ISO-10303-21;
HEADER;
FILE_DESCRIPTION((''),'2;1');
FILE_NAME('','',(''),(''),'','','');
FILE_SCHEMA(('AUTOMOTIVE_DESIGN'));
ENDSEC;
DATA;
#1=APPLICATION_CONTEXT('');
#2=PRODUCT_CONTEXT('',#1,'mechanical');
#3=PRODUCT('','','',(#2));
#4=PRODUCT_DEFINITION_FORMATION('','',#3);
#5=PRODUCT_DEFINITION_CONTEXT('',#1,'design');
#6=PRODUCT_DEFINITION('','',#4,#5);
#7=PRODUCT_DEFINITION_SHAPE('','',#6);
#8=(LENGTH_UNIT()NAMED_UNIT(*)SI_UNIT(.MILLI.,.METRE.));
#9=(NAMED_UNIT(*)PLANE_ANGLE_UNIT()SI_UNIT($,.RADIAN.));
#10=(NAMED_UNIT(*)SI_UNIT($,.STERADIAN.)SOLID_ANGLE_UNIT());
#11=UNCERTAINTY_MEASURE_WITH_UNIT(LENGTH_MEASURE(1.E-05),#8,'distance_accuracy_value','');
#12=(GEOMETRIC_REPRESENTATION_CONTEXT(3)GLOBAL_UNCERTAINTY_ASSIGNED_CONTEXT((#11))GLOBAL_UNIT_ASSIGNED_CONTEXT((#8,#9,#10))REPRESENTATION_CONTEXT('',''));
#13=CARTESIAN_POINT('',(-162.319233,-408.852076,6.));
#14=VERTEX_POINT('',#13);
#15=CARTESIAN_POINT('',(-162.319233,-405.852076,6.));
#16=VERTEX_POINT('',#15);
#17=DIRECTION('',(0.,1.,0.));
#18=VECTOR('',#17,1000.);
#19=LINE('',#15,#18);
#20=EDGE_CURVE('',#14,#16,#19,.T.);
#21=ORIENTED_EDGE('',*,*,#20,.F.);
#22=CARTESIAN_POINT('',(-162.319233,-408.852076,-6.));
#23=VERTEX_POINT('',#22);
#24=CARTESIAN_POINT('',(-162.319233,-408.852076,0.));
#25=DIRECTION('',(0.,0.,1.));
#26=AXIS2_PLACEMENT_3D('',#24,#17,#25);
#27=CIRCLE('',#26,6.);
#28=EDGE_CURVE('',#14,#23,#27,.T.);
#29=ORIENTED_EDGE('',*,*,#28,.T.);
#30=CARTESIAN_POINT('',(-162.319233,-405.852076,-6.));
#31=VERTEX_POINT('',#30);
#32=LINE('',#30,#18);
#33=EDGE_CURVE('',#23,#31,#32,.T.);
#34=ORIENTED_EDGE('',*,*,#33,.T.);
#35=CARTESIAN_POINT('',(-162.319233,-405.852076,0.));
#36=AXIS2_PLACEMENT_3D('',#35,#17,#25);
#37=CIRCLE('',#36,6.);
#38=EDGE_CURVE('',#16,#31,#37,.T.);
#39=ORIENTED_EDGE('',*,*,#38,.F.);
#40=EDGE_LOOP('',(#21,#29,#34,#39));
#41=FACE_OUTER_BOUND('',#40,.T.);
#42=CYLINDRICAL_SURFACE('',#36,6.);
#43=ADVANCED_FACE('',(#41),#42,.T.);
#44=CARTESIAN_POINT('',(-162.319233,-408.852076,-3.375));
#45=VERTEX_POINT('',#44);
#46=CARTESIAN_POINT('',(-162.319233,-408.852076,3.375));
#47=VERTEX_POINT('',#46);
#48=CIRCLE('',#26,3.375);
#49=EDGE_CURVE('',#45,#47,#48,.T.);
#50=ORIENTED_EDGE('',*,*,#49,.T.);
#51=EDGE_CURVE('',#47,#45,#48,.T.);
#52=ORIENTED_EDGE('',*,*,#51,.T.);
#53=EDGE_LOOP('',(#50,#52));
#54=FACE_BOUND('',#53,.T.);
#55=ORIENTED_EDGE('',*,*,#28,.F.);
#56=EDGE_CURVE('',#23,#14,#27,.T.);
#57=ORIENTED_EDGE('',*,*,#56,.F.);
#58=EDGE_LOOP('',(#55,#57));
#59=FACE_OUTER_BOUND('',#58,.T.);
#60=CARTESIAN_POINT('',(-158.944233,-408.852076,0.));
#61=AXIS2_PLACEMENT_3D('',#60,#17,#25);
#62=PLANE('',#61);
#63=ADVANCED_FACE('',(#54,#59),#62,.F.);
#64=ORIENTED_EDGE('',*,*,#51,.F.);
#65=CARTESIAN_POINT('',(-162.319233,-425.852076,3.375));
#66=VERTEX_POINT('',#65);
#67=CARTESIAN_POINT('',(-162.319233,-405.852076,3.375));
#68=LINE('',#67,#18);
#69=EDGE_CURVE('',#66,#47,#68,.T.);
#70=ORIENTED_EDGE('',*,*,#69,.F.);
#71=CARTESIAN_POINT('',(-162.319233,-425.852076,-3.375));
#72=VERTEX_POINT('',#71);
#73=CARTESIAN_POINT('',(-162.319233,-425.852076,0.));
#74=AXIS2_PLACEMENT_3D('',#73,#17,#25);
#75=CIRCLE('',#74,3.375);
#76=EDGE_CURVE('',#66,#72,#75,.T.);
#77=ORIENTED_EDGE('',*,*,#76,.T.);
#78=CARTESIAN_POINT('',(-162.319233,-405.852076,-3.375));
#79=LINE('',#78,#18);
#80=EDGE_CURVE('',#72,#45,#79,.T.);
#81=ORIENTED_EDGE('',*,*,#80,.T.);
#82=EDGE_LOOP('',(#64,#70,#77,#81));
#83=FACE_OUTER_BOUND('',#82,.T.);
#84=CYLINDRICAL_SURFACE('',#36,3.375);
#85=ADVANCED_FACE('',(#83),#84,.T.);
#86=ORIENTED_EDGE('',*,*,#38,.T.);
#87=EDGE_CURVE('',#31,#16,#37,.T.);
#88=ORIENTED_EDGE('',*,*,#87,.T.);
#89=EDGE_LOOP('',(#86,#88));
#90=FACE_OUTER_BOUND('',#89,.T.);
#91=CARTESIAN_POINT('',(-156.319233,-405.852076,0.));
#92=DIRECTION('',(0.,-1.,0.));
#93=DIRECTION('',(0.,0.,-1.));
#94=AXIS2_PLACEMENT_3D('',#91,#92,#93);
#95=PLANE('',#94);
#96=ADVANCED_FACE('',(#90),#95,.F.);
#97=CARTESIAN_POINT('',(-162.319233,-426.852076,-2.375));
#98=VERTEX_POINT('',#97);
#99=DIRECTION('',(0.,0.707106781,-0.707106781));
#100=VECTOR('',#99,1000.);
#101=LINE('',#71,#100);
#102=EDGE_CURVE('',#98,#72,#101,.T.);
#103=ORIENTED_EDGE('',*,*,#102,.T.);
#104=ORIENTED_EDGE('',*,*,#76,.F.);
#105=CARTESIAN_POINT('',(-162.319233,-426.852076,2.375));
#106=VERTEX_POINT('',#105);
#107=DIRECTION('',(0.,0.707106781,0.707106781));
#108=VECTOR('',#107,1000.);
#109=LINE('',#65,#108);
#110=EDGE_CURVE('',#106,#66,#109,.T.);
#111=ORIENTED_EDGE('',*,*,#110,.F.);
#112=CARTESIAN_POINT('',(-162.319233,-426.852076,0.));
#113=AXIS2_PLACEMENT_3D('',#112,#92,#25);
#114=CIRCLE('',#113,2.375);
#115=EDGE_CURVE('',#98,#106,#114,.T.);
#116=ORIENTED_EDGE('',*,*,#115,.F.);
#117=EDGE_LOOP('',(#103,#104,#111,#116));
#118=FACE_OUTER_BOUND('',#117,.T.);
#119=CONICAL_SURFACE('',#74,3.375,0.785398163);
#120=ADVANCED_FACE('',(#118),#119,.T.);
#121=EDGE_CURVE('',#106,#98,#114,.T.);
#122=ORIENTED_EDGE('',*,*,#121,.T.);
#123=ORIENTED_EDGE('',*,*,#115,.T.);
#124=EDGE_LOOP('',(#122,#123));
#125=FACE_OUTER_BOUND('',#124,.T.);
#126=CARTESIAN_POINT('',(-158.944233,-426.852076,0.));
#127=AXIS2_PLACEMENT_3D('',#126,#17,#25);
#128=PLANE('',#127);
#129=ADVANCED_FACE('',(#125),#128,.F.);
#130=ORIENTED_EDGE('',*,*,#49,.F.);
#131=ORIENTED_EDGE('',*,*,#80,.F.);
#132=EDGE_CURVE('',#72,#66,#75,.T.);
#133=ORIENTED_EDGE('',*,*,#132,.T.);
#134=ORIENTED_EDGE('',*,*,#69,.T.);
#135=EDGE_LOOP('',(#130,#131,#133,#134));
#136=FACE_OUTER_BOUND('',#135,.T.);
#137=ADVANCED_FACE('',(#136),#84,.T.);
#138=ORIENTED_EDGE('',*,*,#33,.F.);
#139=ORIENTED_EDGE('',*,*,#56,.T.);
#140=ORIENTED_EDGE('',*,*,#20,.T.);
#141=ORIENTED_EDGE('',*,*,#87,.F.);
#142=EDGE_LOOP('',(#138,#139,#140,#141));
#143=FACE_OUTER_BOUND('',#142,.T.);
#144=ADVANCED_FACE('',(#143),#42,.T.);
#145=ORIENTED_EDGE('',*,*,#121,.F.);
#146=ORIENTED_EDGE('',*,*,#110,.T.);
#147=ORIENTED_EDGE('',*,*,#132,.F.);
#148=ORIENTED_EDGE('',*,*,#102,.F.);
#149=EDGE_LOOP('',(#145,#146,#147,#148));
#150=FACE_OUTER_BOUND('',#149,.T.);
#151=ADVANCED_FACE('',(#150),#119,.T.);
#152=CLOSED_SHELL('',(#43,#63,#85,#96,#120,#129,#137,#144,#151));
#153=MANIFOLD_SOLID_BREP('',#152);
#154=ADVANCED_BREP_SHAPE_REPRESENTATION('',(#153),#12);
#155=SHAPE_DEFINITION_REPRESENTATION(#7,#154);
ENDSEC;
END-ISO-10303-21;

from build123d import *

# Parameters (mm, degrees)
CHAMFER1_SIZE = 1


with BuildPart() as part:
    # Sketch1 → Revolve2 (revolve)
    with BuildSketch(Plane.XY, mode=Mode.PRIVATE) as revolve2_sk:
        Polygon((-158.944232661, -426.85207641), (-162.319232661, -426.85207641), (-162.319232661, -405.85207641), (-156.319232661, -405.85207641), (-156.319232661, -408.85207641), (-158.944232661, -408.85207641), align=None)
    revolve(revolve2_sk.sketch.rotate(Axis((-162.319232661, -405.85207641, 0), (0, -1, 0)), 90), axis=Axis((-162.319232661, -405.85207641, 0), (0, -1, 0)))

    # Chamfer1
    chamfer1_edges = [part.edges().sort_by_distance(p)[0] for p in [
        (-162.319232661, -426.85207641, -3.375),
    ]]
    chamfer(chamfer1_edges, length=CHAMFER1_SIZE)


solid = part.part
